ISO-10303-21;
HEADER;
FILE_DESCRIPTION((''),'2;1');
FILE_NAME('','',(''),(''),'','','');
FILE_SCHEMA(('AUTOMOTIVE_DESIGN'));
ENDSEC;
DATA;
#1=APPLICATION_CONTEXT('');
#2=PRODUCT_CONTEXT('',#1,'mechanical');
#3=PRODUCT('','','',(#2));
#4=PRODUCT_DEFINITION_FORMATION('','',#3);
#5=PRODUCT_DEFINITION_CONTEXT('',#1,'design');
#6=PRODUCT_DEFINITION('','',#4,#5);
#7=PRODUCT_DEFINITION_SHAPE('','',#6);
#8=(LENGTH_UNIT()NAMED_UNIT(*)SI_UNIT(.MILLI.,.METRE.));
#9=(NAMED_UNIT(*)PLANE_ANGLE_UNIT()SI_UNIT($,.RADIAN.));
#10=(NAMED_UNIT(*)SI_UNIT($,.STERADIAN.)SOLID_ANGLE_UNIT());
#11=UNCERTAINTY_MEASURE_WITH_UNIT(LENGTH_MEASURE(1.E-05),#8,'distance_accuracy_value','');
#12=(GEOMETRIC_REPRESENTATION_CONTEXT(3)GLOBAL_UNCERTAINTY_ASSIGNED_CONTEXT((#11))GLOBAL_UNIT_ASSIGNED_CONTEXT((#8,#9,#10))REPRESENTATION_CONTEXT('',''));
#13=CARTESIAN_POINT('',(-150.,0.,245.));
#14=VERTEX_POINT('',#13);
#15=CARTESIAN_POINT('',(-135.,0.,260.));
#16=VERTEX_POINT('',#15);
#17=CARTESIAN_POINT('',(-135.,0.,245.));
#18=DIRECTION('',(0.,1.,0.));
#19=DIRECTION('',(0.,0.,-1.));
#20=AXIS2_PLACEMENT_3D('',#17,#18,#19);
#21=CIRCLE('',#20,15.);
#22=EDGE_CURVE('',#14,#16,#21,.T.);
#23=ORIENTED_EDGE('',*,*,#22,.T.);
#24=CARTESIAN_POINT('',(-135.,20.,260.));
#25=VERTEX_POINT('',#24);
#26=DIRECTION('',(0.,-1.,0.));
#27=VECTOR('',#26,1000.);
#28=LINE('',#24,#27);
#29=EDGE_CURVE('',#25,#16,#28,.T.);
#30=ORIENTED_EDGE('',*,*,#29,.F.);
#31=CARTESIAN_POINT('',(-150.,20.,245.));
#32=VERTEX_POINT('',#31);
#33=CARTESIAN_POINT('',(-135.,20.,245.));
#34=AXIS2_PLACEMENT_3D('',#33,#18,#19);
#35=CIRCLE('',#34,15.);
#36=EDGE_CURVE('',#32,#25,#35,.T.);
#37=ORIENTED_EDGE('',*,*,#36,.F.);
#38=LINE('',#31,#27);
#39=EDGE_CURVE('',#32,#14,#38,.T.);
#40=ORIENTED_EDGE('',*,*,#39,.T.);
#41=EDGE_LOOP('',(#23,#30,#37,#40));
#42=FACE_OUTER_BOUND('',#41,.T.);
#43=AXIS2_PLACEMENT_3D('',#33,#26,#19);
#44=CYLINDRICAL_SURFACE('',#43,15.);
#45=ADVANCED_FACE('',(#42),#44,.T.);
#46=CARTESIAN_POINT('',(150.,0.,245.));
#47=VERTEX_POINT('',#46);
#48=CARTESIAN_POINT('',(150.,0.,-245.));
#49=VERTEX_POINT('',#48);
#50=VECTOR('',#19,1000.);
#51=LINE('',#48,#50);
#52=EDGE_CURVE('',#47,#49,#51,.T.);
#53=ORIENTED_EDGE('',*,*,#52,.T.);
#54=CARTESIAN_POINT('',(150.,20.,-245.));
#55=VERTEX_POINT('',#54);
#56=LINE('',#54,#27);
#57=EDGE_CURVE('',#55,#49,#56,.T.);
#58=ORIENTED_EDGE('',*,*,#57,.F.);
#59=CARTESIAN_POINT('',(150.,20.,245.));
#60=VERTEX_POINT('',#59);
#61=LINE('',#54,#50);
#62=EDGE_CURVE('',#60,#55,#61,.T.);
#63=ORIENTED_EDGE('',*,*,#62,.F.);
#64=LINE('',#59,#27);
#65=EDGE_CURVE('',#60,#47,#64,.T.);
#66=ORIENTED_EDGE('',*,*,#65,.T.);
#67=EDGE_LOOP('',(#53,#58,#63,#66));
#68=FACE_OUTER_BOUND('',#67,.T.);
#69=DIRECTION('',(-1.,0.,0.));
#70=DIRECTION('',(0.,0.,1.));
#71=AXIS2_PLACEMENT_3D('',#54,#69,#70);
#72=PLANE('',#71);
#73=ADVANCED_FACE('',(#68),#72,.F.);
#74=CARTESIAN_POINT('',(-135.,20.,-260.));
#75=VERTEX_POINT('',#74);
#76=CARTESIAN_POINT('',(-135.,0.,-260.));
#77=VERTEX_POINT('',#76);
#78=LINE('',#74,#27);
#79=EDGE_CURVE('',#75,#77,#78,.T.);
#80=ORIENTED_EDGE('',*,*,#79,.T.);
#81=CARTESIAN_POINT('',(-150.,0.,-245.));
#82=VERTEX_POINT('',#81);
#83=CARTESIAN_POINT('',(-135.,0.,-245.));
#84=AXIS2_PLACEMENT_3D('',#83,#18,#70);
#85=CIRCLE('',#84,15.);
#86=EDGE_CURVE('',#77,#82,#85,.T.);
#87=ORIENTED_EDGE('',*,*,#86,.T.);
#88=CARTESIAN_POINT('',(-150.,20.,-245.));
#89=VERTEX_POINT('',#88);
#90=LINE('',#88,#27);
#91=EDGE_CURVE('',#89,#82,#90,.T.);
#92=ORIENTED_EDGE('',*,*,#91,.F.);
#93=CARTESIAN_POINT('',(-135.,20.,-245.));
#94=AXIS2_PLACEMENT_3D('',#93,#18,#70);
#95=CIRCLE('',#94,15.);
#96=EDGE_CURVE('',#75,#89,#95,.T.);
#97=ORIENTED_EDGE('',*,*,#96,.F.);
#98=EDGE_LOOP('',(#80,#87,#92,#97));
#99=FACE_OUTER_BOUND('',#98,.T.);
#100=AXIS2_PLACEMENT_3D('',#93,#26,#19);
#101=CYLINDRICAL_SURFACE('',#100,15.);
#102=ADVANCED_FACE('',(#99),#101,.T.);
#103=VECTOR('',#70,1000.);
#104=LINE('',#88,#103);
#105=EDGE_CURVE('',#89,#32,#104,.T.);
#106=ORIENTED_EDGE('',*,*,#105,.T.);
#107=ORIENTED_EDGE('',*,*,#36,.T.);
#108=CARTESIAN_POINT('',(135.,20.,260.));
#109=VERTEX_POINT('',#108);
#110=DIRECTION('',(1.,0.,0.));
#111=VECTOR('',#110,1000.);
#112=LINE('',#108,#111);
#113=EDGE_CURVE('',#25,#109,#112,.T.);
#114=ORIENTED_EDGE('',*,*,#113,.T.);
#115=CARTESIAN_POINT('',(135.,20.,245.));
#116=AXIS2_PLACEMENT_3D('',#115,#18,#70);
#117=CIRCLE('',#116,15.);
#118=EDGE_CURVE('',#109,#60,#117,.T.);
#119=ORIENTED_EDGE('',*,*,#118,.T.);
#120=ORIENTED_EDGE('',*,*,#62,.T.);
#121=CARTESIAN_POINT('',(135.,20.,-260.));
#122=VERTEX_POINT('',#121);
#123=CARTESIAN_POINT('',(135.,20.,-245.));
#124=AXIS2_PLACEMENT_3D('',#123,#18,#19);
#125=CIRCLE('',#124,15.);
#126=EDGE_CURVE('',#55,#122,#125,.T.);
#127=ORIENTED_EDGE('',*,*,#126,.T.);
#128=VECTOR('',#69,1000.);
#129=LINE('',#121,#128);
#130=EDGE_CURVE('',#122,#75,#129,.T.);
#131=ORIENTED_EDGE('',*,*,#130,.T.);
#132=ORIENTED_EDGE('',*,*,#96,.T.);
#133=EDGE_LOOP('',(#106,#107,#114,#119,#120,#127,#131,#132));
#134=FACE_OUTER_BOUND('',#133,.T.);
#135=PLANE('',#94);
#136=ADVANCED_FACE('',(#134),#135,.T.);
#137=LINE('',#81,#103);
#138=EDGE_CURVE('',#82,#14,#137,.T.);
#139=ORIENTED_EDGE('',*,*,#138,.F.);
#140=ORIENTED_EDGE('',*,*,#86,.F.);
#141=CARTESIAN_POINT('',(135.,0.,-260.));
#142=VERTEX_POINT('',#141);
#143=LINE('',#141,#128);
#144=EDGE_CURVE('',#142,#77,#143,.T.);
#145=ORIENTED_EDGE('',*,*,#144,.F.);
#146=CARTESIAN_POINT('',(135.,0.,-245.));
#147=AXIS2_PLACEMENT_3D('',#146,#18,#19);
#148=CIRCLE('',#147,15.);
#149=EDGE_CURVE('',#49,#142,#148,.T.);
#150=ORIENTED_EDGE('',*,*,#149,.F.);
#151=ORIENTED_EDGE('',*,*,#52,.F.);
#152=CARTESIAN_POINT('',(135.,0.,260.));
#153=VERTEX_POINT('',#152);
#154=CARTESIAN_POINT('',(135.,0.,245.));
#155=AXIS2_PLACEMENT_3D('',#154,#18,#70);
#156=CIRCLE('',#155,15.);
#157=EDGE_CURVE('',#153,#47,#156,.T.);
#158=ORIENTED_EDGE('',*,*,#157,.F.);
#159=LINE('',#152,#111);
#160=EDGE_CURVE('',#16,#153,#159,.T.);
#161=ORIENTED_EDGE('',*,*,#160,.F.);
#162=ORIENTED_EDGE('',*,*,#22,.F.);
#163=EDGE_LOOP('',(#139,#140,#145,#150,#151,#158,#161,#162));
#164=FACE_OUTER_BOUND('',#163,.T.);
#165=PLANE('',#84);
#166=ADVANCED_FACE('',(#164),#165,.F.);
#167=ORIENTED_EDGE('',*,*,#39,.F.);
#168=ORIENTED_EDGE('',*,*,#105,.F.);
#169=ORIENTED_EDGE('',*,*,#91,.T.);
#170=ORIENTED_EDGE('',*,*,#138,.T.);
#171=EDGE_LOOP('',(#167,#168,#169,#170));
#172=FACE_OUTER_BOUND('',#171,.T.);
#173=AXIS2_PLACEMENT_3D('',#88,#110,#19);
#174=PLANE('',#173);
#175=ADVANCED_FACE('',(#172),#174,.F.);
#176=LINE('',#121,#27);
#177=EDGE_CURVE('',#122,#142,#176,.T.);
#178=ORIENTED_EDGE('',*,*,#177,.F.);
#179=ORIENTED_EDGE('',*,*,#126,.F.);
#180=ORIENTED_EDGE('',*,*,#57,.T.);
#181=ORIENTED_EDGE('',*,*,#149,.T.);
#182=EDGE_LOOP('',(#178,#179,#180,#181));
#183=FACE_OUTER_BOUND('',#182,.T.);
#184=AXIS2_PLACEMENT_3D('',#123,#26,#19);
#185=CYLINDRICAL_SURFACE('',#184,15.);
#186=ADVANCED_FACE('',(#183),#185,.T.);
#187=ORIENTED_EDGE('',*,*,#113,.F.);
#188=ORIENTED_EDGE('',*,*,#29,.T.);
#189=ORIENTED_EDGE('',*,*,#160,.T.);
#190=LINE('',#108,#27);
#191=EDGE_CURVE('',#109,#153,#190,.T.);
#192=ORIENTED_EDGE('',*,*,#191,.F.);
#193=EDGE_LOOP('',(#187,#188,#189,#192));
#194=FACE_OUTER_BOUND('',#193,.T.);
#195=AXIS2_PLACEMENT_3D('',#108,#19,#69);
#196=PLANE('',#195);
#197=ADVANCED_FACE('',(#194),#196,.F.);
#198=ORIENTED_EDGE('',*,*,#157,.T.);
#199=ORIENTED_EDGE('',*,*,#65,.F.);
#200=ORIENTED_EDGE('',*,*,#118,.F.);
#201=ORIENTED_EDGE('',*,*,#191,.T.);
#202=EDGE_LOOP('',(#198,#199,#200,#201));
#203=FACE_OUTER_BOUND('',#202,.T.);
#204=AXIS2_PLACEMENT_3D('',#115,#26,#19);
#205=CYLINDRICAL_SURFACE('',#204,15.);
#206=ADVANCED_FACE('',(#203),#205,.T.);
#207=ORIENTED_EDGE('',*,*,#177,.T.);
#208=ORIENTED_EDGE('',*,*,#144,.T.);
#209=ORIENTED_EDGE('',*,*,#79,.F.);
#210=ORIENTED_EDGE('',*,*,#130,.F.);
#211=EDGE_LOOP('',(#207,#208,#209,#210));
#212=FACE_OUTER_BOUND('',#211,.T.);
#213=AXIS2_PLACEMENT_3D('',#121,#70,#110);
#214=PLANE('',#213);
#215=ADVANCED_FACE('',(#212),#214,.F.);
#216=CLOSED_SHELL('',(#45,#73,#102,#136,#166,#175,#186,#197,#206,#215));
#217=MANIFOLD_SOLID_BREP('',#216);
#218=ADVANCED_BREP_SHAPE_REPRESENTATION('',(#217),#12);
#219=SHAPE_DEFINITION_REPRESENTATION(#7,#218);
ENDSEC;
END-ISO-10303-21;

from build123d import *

# Parameters (mm, degrees)
BOSS_EXTRUDE_1_DEPTH = 20


with BuildPart() as part:
    # Sketch 1 → Boss-Extrude 1 (new body)
    with BuildSketch(Plane(origin=(0, 0, 0), x_dir=(1, 0, 0), z_dir=(0, 1, 0))):
        with BuildLine():
            Line((135, 260), (-135, 260))
            ThreePointArc((-135, 260), (-145.606601718, 255.606601718), (-150, 245))
            Line((-150, 245), (-150, -245))
            ThreePointArc((-150, -245), (-145.606601718, -255.606601718), (-135, -260))
            Line((-135, -260), (135, -260))
            ThreePointArc((135, -260), (145.606601718, -255.606601718), (150, -245))
            Line((150, -245), (150, 245))
            ThreePointArc((150, 245), (145.606601718, 255.606601718), (135, 260))
        make_face()
    extrude(amount=BOSS_EXTRUDE_1_DEPTH)


solid = part.part
